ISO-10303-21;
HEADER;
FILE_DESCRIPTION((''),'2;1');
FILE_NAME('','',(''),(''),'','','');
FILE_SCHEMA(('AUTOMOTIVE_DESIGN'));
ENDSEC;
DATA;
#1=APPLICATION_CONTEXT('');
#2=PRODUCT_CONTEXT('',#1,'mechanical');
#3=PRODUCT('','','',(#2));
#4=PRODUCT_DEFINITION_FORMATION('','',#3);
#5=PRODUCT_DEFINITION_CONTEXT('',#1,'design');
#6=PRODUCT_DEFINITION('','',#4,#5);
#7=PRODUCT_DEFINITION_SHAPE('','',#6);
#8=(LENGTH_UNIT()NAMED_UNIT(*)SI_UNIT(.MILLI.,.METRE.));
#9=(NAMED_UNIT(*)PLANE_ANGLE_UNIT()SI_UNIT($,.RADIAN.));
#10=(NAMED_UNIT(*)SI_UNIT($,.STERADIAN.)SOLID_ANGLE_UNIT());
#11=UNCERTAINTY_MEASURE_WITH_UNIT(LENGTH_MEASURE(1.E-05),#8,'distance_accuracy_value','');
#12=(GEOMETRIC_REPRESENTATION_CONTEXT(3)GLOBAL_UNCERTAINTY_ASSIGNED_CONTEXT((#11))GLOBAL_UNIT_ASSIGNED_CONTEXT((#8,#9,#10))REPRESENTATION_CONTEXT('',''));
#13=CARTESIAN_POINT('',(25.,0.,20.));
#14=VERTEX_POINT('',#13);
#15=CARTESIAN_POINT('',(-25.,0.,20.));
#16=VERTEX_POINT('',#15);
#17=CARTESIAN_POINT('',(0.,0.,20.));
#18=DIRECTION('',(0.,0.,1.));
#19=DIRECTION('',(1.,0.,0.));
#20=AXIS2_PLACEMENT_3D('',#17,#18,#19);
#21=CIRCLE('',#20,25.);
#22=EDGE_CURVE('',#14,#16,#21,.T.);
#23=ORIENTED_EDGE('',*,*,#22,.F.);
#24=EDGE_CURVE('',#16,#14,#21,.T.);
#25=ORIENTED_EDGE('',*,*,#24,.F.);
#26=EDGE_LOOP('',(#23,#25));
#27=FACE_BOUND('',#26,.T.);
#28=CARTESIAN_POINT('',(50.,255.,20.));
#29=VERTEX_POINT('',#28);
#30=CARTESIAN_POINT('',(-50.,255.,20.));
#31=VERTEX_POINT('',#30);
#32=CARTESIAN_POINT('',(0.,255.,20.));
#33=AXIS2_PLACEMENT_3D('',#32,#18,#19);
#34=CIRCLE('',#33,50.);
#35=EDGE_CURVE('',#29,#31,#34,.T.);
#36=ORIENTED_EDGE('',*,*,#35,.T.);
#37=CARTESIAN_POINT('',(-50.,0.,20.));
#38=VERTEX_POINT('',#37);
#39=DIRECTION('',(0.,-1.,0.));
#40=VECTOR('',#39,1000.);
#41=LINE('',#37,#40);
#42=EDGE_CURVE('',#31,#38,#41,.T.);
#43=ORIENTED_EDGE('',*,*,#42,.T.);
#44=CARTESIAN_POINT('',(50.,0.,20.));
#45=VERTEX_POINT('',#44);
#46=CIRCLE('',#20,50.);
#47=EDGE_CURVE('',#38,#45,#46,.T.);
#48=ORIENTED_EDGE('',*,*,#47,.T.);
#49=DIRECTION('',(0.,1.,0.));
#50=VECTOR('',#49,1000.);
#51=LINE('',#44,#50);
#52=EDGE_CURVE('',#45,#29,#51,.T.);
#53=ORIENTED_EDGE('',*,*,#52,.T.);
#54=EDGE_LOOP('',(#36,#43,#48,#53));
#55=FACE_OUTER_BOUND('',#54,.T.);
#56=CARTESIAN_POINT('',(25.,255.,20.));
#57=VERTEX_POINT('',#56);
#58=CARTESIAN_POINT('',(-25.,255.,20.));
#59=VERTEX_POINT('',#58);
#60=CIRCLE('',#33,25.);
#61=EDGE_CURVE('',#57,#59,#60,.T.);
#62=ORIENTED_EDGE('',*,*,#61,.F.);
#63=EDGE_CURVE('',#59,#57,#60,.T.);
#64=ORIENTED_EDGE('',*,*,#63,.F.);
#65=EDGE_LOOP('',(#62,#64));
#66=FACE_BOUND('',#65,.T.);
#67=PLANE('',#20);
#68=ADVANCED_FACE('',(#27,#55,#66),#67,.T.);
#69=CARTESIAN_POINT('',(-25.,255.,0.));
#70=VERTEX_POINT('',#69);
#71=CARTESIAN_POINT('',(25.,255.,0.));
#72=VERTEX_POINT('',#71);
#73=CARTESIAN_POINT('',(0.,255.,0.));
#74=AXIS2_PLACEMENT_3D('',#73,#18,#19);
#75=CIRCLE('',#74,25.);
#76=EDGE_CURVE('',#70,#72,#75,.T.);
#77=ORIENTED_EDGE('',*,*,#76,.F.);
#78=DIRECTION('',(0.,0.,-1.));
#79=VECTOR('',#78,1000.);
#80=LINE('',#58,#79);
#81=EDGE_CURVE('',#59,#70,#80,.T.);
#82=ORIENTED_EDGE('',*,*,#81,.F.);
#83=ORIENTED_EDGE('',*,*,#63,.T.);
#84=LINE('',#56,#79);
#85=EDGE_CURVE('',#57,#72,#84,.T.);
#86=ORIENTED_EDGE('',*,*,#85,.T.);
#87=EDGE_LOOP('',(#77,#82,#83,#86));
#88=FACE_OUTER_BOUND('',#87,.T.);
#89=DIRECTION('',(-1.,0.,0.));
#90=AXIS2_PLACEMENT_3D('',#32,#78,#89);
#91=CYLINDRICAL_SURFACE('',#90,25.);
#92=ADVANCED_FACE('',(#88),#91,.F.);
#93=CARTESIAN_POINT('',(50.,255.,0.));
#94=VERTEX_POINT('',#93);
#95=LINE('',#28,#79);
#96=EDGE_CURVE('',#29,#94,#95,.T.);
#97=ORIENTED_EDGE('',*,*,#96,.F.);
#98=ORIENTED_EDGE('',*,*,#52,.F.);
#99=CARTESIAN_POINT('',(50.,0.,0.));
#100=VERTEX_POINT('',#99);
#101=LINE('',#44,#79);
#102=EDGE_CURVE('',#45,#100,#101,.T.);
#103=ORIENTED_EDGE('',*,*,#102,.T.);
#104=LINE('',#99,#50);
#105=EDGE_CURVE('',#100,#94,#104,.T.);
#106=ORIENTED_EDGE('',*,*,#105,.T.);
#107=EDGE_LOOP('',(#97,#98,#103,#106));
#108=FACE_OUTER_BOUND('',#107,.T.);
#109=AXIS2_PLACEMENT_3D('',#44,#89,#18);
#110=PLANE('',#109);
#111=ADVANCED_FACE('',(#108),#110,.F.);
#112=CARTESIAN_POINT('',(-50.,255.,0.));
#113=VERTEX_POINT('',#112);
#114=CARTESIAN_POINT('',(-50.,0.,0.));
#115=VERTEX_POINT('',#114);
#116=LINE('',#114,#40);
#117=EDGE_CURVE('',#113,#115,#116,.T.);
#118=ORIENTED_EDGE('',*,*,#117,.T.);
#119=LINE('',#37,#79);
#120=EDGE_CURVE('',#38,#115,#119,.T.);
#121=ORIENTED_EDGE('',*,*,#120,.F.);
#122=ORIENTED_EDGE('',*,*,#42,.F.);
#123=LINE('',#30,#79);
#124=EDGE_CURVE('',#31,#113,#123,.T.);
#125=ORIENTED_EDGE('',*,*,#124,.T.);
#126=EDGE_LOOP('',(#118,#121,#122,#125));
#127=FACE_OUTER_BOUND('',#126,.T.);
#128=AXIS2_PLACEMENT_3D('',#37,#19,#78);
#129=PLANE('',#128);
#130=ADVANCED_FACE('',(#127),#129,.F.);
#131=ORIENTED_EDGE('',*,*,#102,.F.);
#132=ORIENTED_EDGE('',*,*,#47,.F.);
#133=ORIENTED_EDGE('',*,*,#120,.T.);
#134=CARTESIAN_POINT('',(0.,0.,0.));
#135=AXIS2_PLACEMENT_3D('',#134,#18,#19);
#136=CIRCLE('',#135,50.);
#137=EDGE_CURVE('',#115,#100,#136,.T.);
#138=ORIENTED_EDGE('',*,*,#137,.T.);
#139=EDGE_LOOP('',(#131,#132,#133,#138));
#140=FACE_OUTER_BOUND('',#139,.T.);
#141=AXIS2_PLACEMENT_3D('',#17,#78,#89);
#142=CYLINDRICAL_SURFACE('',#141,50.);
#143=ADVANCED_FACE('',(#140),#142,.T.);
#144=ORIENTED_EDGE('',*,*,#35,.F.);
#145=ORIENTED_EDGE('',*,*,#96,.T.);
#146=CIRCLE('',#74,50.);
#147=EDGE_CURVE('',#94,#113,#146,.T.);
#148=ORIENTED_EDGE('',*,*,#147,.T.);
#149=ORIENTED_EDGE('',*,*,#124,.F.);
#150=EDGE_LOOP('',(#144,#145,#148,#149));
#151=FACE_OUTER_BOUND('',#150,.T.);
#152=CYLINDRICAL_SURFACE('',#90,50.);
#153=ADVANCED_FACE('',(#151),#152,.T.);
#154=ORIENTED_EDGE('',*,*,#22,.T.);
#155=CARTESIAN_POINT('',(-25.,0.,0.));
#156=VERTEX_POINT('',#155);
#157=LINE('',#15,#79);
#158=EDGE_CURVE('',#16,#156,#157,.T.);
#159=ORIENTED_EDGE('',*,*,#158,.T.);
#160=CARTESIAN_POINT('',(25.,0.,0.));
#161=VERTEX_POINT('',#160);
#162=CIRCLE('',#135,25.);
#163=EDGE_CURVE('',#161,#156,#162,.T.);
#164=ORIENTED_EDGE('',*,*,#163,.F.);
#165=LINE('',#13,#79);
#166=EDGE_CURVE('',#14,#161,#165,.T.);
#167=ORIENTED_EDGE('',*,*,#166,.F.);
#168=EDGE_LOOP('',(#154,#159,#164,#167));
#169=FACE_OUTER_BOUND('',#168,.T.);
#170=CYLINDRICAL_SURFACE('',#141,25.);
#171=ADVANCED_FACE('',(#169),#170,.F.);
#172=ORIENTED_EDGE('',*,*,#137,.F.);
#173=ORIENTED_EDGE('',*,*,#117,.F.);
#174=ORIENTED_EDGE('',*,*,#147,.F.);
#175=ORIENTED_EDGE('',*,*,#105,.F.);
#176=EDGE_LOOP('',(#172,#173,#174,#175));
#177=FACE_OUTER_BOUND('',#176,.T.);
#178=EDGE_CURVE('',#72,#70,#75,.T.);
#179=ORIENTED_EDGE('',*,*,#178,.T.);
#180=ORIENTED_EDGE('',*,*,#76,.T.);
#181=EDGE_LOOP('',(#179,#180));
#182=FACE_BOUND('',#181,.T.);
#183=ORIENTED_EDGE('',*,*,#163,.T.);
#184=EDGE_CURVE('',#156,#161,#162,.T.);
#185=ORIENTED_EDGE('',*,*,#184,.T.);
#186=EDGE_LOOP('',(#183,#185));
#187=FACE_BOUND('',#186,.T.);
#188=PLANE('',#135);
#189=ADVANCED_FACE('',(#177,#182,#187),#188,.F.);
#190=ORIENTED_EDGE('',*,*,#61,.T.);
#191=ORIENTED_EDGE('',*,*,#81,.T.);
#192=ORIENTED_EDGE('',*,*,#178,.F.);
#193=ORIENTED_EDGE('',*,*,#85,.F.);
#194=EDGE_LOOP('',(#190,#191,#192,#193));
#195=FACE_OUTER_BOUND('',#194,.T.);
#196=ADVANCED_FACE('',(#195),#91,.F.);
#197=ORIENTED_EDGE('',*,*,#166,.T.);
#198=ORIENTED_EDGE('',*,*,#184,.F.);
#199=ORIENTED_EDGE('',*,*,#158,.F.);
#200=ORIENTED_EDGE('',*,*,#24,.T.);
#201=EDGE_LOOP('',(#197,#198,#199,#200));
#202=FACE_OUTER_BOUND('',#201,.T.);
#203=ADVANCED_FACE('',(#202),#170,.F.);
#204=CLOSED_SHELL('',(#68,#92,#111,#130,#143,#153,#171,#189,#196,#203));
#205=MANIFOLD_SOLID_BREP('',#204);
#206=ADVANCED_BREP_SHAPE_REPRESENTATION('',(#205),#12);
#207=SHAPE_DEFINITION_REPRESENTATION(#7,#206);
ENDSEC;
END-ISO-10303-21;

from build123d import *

# Parameters (mm, degrees)
LINK_BAR_PROFILE_R  = 25
LINK_BAR_20MM_DEPTH = 20


with BuildPart() as part:
    # Link Bar Profile → Link Bar 20mm (new body)
    with BuildSketch(Plane.XY):
        with BuildLine():
            Line((-50, 0), (-50, 255))
            ThreePointArc((-50, 255), (0, 305), (50, 255))
            Line((50, 255), (50, 0))
            ThreePointArc((50, 0), (0, -50), (-50, 0))
        make_face()
        with Locations((0, 255)):
            Circle(LINK_BAR_PROFILE_R, mode=Mode.SUBTRACT)
        Circle(LINK_BAR_PROFILE_R, mode=Mode.SUBTRACT)
    extrude(amount=LINK_BAR_20MM_DEPTH)


solid = part.part
